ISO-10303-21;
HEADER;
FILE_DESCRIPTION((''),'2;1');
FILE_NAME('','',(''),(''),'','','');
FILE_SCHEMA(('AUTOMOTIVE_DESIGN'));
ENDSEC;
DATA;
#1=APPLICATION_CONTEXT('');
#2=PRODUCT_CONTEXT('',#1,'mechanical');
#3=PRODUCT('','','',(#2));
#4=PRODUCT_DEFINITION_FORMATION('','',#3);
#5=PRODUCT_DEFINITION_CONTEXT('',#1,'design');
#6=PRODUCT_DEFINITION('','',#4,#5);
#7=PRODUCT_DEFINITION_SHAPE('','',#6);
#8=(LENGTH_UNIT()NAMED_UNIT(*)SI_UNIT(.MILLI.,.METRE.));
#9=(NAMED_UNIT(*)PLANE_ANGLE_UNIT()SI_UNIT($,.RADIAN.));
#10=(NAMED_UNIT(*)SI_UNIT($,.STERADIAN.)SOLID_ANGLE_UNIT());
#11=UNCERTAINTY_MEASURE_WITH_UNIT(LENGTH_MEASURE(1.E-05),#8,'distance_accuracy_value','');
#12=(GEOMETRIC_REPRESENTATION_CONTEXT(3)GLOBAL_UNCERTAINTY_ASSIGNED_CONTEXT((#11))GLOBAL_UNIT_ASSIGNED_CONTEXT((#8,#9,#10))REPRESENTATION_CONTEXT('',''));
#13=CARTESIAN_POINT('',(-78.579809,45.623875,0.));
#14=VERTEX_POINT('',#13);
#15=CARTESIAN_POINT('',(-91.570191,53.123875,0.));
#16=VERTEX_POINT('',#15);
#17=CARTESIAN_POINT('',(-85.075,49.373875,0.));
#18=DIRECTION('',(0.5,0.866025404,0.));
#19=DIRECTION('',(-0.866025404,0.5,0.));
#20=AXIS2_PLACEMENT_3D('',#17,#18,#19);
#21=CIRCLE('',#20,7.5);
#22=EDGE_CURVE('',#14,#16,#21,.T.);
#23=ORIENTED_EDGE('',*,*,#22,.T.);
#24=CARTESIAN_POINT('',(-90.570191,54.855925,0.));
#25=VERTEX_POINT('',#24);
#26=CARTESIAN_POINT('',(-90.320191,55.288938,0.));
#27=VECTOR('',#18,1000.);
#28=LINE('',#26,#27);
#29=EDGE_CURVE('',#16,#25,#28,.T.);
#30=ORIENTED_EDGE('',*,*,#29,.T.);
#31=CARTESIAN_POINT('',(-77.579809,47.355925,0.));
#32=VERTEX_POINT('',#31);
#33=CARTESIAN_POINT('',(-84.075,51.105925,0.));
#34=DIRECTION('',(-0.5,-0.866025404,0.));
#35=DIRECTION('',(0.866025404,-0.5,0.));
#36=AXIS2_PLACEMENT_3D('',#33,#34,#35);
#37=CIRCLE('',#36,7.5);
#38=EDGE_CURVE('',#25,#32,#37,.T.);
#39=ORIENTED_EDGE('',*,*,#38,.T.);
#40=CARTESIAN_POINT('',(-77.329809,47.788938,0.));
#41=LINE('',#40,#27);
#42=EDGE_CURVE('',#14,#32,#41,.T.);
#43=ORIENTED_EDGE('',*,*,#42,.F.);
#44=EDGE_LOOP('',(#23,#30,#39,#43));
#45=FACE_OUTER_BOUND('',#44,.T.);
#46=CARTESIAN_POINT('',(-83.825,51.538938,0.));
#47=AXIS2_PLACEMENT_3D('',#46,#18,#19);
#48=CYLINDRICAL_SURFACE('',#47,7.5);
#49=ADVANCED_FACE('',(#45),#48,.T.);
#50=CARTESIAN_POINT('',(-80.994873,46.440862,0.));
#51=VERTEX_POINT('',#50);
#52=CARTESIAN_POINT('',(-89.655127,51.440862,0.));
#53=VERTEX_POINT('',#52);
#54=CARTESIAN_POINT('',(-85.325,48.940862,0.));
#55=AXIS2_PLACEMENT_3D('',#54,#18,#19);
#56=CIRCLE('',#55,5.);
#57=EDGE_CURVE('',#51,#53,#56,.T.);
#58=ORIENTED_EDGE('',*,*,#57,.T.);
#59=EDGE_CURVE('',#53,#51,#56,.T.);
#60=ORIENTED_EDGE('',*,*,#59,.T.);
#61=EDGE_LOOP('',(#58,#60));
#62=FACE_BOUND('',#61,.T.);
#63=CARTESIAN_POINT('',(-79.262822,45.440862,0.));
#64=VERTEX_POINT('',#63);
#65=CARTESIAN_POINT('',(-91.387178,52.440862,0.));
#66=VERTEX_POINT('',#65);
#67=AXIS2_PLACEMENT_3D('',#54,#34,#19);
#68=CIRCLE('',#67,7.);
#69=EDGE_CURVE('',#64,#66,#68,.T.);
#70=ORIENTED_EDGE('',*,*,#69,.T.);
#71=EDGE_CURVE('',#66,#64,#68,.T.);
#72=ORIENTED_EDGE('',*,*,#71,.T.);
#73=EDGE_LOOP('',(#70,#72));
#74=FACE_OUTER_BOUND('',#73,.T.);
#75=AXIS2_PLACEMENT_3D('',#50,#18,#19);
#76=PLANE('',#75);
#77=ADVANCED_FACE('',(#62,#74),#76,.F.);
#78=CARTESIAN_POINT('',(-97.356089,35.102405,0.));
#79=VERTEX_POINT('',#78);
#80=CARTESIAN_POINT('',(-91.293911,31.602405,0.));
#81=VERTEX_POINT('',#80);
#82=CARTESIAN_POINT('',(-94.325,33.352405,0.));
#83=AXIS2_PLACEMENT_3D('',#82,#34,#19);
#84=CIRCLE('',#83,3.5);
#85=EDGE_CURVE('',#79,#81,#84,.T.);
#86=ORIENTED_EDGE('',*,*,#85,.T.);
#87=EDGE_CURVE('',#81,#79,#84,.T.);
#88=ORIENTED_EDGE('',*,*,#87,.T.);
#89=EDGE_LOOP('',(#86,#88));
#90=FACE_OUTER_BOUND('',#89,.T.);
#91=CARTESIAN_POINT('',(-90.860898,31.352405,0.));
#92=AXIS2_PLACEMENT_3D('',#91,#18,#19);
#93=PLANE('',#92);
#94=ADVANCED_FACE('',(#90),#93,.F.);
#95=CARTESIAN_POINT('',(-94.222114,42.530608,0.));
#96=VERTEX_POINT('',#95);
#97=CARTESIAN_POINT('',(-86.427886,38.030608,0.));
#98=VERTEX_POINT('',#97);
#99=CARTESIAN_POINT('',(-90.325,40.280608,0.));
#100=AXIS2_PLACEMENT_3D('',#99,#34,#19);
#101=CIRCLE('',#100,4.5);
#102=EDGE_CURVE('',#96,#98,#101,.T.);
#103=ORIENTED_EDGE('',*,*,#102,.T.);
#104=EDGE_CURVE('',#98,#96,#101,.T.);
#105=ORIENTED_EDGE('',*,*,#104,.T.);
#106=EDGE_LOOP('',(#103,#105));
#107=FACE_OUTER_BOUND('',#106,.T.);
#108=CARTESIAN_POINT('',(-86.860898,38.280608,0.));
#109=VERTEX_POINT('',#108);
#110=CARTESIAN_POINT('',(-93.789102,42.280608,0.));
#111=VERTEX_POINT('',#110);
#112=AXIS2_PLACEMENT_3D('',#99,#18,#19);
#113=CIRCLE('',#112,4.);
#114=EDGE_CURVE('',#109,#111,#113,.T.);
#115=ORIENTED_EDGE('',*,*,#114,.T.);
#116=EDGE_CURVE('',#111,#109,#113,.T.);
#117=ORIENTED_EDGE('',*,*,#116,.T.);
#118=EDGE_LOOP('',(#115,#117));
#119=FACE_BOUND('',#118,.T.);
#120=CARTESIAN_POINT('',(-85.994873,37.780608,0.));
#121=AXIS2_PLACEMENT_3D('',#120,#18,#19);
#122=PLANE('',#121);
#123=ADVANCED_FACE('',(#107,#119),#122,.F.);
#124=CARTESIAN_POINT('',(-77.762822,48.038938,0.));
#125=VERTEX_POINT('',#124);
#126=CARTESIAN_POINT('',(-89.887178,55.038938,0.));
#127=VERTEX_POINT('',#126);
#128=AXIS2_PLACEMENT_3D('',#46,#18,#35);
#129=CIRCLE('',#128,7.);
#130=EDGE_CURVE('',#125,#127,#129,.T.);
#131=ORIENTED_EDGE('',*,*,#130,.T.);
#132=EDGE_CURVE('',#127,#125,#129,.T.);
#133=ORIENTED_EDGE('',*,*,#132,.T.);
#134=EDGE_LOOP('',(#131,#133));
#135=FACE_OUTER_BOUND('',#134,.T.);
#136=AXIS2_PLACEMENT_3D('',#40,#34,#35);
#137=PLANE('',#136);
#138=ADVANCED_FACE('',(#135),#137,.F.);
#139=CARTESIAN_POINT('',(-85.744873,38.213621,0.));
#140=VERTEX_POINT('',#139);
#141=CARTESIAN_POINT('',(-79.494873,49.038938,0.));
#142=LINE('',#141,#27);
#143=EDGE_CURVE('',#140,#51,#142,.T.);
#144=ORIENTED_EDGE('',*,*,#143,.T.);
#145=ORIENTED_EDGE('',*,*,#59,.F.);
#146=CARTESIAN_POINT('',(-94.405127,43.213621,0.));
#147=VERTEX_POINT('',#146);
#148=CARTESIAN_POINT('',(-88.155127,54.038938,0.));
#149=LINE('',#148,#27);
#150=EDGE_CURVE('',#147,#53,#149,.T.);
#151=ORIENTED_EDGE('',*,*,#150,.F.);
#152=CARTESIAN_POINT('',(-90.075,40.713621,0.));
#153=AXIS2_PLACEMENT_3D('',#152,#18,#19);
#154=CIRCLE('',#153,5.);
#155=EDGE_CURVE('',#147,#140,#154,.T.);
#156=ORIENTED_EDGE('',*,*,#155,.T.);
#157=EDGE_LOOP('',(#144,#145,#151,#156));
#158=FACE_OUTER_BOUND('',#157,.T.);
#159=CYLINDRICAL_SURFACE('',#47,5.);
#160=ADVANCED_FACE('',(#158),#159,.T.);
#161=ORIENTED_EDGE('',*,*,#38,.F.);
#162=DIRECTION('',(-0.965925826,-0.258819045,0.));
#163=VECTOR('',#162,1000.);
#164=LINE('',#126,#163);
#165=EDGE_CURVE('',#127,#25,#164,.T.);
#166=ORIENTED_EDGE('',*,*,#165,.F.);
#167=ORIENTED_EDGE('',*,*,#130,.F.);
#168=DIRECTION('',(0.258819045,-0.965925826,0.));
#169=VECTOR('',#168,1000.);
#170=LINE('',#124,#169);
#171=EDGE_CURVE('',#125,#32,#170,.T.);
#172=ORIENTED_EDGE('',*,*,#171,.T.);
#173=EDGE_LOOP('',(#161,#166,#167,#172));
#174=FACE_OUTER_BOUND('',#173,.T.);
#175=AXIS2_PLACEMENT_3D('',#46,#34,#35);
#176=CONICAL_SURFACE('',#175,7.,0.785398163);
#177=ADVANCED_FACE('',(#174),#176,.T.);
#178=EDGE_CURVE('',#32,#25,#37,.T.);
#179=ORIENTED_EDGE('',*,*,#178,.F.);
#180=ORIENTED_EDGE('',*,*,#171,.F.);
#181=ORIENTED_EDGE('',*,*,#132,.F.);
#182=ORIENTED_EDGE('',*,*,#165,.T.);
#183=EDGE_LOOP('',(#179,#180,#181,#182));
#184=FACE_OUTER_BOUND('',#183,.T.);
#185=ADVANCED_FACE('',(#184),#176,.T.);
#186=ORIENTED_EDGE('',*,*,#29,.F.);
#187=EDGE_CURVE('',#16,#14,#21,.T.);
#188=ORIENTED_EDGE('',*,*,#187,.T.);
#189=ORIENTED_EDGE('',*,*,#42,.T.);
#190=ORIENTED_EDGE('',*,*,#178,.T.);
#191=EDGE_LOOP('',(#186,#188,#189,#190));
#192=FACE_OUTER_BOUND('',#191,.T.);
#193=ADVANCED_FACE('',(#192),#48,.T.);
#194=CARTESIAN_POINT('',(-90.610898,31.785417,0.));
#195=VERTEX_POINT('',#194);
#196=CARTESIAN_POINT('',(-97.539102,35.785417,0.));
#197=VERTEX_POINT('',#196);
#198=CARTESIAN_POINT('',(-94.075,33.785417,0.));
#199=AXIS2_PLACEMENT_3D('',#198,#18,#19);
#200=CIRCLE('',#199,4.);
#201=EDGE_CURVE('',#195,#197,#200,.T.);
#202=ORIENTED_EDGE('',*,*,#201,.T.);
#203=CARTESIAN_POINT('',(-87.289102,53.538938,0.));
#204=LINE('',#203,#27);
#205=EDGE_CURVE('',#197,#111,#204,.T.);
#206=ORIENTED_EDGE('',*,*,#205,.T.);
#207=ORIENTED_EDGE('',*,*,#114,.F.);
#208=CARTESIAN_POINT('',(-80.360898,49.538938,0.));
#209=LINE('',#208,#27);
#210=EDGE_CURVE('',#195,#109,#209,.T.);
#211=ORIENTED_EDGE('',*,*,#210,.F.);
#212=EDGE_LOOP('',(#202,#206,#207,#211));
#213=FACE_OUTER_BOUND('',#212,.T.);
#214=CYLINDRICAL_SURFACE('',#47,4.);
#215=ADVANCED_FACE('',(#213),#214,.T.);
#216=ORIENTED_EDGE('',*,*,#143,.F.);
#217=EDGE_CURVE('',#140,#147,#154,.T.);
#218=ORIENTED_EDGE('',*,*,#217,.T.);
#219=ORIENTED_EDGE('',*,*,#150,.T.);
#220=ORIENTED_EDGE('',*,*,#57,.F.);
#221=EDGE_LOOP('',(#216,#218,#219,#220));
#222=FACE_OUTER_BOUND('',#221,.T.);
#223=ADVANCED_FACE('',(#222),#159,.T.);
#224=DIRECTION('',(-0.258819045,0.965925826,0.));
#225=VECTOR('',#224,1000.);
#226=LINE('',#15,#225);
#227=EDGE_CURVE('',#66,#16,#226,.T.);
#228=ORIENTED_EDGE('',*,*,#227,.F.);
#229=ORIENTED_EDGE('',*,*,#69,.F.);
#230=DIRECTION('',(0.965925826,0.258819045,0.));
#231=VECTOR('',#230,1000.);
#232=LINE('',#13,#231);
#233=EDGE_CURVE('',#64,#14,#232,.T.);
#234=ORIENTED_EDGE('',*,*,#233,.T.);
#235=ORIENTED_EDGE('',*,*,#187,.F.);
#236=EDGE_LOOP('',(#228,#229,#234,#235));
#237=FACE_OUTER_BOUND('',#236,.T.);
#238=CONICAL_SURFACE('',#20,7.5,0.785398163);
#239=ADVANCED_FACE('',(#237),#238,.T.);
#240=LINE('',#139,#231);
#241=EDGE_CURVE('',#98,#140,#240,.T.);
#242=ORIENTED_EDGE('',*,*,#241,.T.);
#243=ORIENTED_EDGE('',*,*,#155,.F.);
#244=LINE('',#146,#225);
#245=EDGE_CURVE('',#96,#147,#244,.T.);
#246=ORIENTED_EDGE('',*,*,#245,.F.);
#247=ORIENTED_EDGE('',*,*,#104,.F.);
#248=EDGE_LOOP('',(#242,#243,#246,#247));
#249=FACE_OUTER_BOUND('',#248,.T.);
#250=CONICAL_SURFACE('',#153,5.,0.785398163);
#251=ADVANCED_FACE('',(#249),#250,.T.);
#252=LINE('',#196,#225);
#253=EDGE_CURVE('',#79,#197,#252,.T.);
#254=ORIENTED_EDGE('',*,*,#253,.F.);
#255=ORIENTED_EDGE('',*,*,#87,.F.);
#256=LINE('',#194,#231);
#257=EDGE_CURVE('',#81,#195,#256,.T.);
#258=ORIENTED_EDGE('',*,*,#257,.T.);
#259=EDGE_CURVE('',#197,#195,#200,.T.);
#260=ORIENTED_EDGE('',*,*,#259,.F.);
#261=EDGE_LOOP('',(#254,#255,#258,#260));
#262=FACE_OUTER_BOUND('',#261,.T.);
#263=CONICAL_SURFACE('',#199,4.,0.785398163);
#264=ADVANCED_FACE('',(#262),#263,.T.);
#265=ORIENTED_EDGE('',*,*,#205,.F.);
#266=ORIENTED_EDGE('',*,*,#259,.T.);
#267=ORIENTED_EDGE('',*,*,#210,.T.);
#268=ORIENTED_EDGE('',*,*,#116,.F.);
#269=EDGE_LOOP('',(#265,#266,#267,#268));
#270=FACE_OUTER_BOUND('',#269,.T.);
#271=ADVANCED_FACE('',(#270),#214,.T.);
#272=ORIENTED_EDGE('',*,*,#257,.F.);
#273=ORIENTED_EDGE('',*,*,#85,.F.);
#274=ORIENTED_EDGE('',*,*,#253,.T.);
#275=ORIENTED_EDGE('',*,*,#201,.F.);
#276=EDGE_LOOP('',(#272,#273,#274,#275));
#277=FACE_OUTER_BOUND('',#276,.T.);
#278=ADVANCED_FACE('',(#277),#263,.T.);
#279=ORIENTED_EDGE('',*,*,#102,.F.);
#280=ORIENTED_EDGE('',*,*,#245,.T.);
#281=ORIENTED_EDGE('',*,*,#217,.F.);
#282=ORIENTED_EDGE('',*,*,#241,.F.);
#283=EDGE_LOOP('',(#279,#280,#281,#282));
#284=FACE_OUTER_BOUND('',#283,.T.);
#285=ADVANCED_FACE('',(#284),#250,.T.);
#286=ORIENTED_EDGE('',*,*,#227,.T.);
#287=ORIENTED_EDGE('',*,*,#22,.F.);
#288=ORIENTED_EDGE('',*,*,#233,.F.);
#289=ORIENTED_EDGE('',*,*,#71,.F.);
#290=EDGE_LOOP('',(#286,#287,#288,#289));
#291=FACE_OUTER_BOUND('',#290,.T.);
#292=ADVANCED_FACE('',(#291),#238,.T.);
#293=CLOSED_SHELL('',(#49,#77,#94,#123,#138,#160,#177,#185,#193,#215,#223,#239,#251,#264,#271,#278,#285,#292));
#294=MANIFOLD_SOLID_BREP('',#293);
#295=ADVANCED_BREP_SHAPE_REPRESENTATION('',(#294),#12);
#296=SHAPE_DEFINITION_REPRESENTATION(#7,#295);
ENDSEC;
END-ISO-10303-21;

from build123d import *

# Parameters (mm, degrees)
CHAMFER1_SIZE = 0.5


with BuildPart() as part:
    # Sketch1 → Revolve1 (revolve)
    with BuildSketch(Plane.XY, mode=Mode.PRIVATE) as revolve1_sk:
        Polygon((-80.994872981, 46.440861912), (-78.829809472, 45.190861912), (-77.329809472, 47.788938123), (-83.825, 51.538938123), (-94.325, 33.352404644), (-90.860898385, 31.352404644), (-86.860898385, 38.280607874), (-85.994872981, 37.780607874), align=None)
    revolve(revolve1_sk.sketch.rotate(Axis((-83.825, 51.538938123, 0), (-0.499999999999998, -0.8660254037844399, 0)), 180), axis=Axis((-83.825, 51.538938123, 0), (-0.499999999999998, -0.8660254037844399, 0)))

    # Chamfer1
    chamfer1_edges = [part.edges().sort_by_distance(p)[0] for p in [
        (-85.994872981, 37.780607874, 0),
        (-90.860898385, 31.352404644, 0),
        (-77.329809472, 47.788938123, 0),
        (-78.829809472, 45.190861912, 0),
    ]]
    chamfer(chamfer1_edges, length=CHAMFER1_SIZE)


solid = part.part
